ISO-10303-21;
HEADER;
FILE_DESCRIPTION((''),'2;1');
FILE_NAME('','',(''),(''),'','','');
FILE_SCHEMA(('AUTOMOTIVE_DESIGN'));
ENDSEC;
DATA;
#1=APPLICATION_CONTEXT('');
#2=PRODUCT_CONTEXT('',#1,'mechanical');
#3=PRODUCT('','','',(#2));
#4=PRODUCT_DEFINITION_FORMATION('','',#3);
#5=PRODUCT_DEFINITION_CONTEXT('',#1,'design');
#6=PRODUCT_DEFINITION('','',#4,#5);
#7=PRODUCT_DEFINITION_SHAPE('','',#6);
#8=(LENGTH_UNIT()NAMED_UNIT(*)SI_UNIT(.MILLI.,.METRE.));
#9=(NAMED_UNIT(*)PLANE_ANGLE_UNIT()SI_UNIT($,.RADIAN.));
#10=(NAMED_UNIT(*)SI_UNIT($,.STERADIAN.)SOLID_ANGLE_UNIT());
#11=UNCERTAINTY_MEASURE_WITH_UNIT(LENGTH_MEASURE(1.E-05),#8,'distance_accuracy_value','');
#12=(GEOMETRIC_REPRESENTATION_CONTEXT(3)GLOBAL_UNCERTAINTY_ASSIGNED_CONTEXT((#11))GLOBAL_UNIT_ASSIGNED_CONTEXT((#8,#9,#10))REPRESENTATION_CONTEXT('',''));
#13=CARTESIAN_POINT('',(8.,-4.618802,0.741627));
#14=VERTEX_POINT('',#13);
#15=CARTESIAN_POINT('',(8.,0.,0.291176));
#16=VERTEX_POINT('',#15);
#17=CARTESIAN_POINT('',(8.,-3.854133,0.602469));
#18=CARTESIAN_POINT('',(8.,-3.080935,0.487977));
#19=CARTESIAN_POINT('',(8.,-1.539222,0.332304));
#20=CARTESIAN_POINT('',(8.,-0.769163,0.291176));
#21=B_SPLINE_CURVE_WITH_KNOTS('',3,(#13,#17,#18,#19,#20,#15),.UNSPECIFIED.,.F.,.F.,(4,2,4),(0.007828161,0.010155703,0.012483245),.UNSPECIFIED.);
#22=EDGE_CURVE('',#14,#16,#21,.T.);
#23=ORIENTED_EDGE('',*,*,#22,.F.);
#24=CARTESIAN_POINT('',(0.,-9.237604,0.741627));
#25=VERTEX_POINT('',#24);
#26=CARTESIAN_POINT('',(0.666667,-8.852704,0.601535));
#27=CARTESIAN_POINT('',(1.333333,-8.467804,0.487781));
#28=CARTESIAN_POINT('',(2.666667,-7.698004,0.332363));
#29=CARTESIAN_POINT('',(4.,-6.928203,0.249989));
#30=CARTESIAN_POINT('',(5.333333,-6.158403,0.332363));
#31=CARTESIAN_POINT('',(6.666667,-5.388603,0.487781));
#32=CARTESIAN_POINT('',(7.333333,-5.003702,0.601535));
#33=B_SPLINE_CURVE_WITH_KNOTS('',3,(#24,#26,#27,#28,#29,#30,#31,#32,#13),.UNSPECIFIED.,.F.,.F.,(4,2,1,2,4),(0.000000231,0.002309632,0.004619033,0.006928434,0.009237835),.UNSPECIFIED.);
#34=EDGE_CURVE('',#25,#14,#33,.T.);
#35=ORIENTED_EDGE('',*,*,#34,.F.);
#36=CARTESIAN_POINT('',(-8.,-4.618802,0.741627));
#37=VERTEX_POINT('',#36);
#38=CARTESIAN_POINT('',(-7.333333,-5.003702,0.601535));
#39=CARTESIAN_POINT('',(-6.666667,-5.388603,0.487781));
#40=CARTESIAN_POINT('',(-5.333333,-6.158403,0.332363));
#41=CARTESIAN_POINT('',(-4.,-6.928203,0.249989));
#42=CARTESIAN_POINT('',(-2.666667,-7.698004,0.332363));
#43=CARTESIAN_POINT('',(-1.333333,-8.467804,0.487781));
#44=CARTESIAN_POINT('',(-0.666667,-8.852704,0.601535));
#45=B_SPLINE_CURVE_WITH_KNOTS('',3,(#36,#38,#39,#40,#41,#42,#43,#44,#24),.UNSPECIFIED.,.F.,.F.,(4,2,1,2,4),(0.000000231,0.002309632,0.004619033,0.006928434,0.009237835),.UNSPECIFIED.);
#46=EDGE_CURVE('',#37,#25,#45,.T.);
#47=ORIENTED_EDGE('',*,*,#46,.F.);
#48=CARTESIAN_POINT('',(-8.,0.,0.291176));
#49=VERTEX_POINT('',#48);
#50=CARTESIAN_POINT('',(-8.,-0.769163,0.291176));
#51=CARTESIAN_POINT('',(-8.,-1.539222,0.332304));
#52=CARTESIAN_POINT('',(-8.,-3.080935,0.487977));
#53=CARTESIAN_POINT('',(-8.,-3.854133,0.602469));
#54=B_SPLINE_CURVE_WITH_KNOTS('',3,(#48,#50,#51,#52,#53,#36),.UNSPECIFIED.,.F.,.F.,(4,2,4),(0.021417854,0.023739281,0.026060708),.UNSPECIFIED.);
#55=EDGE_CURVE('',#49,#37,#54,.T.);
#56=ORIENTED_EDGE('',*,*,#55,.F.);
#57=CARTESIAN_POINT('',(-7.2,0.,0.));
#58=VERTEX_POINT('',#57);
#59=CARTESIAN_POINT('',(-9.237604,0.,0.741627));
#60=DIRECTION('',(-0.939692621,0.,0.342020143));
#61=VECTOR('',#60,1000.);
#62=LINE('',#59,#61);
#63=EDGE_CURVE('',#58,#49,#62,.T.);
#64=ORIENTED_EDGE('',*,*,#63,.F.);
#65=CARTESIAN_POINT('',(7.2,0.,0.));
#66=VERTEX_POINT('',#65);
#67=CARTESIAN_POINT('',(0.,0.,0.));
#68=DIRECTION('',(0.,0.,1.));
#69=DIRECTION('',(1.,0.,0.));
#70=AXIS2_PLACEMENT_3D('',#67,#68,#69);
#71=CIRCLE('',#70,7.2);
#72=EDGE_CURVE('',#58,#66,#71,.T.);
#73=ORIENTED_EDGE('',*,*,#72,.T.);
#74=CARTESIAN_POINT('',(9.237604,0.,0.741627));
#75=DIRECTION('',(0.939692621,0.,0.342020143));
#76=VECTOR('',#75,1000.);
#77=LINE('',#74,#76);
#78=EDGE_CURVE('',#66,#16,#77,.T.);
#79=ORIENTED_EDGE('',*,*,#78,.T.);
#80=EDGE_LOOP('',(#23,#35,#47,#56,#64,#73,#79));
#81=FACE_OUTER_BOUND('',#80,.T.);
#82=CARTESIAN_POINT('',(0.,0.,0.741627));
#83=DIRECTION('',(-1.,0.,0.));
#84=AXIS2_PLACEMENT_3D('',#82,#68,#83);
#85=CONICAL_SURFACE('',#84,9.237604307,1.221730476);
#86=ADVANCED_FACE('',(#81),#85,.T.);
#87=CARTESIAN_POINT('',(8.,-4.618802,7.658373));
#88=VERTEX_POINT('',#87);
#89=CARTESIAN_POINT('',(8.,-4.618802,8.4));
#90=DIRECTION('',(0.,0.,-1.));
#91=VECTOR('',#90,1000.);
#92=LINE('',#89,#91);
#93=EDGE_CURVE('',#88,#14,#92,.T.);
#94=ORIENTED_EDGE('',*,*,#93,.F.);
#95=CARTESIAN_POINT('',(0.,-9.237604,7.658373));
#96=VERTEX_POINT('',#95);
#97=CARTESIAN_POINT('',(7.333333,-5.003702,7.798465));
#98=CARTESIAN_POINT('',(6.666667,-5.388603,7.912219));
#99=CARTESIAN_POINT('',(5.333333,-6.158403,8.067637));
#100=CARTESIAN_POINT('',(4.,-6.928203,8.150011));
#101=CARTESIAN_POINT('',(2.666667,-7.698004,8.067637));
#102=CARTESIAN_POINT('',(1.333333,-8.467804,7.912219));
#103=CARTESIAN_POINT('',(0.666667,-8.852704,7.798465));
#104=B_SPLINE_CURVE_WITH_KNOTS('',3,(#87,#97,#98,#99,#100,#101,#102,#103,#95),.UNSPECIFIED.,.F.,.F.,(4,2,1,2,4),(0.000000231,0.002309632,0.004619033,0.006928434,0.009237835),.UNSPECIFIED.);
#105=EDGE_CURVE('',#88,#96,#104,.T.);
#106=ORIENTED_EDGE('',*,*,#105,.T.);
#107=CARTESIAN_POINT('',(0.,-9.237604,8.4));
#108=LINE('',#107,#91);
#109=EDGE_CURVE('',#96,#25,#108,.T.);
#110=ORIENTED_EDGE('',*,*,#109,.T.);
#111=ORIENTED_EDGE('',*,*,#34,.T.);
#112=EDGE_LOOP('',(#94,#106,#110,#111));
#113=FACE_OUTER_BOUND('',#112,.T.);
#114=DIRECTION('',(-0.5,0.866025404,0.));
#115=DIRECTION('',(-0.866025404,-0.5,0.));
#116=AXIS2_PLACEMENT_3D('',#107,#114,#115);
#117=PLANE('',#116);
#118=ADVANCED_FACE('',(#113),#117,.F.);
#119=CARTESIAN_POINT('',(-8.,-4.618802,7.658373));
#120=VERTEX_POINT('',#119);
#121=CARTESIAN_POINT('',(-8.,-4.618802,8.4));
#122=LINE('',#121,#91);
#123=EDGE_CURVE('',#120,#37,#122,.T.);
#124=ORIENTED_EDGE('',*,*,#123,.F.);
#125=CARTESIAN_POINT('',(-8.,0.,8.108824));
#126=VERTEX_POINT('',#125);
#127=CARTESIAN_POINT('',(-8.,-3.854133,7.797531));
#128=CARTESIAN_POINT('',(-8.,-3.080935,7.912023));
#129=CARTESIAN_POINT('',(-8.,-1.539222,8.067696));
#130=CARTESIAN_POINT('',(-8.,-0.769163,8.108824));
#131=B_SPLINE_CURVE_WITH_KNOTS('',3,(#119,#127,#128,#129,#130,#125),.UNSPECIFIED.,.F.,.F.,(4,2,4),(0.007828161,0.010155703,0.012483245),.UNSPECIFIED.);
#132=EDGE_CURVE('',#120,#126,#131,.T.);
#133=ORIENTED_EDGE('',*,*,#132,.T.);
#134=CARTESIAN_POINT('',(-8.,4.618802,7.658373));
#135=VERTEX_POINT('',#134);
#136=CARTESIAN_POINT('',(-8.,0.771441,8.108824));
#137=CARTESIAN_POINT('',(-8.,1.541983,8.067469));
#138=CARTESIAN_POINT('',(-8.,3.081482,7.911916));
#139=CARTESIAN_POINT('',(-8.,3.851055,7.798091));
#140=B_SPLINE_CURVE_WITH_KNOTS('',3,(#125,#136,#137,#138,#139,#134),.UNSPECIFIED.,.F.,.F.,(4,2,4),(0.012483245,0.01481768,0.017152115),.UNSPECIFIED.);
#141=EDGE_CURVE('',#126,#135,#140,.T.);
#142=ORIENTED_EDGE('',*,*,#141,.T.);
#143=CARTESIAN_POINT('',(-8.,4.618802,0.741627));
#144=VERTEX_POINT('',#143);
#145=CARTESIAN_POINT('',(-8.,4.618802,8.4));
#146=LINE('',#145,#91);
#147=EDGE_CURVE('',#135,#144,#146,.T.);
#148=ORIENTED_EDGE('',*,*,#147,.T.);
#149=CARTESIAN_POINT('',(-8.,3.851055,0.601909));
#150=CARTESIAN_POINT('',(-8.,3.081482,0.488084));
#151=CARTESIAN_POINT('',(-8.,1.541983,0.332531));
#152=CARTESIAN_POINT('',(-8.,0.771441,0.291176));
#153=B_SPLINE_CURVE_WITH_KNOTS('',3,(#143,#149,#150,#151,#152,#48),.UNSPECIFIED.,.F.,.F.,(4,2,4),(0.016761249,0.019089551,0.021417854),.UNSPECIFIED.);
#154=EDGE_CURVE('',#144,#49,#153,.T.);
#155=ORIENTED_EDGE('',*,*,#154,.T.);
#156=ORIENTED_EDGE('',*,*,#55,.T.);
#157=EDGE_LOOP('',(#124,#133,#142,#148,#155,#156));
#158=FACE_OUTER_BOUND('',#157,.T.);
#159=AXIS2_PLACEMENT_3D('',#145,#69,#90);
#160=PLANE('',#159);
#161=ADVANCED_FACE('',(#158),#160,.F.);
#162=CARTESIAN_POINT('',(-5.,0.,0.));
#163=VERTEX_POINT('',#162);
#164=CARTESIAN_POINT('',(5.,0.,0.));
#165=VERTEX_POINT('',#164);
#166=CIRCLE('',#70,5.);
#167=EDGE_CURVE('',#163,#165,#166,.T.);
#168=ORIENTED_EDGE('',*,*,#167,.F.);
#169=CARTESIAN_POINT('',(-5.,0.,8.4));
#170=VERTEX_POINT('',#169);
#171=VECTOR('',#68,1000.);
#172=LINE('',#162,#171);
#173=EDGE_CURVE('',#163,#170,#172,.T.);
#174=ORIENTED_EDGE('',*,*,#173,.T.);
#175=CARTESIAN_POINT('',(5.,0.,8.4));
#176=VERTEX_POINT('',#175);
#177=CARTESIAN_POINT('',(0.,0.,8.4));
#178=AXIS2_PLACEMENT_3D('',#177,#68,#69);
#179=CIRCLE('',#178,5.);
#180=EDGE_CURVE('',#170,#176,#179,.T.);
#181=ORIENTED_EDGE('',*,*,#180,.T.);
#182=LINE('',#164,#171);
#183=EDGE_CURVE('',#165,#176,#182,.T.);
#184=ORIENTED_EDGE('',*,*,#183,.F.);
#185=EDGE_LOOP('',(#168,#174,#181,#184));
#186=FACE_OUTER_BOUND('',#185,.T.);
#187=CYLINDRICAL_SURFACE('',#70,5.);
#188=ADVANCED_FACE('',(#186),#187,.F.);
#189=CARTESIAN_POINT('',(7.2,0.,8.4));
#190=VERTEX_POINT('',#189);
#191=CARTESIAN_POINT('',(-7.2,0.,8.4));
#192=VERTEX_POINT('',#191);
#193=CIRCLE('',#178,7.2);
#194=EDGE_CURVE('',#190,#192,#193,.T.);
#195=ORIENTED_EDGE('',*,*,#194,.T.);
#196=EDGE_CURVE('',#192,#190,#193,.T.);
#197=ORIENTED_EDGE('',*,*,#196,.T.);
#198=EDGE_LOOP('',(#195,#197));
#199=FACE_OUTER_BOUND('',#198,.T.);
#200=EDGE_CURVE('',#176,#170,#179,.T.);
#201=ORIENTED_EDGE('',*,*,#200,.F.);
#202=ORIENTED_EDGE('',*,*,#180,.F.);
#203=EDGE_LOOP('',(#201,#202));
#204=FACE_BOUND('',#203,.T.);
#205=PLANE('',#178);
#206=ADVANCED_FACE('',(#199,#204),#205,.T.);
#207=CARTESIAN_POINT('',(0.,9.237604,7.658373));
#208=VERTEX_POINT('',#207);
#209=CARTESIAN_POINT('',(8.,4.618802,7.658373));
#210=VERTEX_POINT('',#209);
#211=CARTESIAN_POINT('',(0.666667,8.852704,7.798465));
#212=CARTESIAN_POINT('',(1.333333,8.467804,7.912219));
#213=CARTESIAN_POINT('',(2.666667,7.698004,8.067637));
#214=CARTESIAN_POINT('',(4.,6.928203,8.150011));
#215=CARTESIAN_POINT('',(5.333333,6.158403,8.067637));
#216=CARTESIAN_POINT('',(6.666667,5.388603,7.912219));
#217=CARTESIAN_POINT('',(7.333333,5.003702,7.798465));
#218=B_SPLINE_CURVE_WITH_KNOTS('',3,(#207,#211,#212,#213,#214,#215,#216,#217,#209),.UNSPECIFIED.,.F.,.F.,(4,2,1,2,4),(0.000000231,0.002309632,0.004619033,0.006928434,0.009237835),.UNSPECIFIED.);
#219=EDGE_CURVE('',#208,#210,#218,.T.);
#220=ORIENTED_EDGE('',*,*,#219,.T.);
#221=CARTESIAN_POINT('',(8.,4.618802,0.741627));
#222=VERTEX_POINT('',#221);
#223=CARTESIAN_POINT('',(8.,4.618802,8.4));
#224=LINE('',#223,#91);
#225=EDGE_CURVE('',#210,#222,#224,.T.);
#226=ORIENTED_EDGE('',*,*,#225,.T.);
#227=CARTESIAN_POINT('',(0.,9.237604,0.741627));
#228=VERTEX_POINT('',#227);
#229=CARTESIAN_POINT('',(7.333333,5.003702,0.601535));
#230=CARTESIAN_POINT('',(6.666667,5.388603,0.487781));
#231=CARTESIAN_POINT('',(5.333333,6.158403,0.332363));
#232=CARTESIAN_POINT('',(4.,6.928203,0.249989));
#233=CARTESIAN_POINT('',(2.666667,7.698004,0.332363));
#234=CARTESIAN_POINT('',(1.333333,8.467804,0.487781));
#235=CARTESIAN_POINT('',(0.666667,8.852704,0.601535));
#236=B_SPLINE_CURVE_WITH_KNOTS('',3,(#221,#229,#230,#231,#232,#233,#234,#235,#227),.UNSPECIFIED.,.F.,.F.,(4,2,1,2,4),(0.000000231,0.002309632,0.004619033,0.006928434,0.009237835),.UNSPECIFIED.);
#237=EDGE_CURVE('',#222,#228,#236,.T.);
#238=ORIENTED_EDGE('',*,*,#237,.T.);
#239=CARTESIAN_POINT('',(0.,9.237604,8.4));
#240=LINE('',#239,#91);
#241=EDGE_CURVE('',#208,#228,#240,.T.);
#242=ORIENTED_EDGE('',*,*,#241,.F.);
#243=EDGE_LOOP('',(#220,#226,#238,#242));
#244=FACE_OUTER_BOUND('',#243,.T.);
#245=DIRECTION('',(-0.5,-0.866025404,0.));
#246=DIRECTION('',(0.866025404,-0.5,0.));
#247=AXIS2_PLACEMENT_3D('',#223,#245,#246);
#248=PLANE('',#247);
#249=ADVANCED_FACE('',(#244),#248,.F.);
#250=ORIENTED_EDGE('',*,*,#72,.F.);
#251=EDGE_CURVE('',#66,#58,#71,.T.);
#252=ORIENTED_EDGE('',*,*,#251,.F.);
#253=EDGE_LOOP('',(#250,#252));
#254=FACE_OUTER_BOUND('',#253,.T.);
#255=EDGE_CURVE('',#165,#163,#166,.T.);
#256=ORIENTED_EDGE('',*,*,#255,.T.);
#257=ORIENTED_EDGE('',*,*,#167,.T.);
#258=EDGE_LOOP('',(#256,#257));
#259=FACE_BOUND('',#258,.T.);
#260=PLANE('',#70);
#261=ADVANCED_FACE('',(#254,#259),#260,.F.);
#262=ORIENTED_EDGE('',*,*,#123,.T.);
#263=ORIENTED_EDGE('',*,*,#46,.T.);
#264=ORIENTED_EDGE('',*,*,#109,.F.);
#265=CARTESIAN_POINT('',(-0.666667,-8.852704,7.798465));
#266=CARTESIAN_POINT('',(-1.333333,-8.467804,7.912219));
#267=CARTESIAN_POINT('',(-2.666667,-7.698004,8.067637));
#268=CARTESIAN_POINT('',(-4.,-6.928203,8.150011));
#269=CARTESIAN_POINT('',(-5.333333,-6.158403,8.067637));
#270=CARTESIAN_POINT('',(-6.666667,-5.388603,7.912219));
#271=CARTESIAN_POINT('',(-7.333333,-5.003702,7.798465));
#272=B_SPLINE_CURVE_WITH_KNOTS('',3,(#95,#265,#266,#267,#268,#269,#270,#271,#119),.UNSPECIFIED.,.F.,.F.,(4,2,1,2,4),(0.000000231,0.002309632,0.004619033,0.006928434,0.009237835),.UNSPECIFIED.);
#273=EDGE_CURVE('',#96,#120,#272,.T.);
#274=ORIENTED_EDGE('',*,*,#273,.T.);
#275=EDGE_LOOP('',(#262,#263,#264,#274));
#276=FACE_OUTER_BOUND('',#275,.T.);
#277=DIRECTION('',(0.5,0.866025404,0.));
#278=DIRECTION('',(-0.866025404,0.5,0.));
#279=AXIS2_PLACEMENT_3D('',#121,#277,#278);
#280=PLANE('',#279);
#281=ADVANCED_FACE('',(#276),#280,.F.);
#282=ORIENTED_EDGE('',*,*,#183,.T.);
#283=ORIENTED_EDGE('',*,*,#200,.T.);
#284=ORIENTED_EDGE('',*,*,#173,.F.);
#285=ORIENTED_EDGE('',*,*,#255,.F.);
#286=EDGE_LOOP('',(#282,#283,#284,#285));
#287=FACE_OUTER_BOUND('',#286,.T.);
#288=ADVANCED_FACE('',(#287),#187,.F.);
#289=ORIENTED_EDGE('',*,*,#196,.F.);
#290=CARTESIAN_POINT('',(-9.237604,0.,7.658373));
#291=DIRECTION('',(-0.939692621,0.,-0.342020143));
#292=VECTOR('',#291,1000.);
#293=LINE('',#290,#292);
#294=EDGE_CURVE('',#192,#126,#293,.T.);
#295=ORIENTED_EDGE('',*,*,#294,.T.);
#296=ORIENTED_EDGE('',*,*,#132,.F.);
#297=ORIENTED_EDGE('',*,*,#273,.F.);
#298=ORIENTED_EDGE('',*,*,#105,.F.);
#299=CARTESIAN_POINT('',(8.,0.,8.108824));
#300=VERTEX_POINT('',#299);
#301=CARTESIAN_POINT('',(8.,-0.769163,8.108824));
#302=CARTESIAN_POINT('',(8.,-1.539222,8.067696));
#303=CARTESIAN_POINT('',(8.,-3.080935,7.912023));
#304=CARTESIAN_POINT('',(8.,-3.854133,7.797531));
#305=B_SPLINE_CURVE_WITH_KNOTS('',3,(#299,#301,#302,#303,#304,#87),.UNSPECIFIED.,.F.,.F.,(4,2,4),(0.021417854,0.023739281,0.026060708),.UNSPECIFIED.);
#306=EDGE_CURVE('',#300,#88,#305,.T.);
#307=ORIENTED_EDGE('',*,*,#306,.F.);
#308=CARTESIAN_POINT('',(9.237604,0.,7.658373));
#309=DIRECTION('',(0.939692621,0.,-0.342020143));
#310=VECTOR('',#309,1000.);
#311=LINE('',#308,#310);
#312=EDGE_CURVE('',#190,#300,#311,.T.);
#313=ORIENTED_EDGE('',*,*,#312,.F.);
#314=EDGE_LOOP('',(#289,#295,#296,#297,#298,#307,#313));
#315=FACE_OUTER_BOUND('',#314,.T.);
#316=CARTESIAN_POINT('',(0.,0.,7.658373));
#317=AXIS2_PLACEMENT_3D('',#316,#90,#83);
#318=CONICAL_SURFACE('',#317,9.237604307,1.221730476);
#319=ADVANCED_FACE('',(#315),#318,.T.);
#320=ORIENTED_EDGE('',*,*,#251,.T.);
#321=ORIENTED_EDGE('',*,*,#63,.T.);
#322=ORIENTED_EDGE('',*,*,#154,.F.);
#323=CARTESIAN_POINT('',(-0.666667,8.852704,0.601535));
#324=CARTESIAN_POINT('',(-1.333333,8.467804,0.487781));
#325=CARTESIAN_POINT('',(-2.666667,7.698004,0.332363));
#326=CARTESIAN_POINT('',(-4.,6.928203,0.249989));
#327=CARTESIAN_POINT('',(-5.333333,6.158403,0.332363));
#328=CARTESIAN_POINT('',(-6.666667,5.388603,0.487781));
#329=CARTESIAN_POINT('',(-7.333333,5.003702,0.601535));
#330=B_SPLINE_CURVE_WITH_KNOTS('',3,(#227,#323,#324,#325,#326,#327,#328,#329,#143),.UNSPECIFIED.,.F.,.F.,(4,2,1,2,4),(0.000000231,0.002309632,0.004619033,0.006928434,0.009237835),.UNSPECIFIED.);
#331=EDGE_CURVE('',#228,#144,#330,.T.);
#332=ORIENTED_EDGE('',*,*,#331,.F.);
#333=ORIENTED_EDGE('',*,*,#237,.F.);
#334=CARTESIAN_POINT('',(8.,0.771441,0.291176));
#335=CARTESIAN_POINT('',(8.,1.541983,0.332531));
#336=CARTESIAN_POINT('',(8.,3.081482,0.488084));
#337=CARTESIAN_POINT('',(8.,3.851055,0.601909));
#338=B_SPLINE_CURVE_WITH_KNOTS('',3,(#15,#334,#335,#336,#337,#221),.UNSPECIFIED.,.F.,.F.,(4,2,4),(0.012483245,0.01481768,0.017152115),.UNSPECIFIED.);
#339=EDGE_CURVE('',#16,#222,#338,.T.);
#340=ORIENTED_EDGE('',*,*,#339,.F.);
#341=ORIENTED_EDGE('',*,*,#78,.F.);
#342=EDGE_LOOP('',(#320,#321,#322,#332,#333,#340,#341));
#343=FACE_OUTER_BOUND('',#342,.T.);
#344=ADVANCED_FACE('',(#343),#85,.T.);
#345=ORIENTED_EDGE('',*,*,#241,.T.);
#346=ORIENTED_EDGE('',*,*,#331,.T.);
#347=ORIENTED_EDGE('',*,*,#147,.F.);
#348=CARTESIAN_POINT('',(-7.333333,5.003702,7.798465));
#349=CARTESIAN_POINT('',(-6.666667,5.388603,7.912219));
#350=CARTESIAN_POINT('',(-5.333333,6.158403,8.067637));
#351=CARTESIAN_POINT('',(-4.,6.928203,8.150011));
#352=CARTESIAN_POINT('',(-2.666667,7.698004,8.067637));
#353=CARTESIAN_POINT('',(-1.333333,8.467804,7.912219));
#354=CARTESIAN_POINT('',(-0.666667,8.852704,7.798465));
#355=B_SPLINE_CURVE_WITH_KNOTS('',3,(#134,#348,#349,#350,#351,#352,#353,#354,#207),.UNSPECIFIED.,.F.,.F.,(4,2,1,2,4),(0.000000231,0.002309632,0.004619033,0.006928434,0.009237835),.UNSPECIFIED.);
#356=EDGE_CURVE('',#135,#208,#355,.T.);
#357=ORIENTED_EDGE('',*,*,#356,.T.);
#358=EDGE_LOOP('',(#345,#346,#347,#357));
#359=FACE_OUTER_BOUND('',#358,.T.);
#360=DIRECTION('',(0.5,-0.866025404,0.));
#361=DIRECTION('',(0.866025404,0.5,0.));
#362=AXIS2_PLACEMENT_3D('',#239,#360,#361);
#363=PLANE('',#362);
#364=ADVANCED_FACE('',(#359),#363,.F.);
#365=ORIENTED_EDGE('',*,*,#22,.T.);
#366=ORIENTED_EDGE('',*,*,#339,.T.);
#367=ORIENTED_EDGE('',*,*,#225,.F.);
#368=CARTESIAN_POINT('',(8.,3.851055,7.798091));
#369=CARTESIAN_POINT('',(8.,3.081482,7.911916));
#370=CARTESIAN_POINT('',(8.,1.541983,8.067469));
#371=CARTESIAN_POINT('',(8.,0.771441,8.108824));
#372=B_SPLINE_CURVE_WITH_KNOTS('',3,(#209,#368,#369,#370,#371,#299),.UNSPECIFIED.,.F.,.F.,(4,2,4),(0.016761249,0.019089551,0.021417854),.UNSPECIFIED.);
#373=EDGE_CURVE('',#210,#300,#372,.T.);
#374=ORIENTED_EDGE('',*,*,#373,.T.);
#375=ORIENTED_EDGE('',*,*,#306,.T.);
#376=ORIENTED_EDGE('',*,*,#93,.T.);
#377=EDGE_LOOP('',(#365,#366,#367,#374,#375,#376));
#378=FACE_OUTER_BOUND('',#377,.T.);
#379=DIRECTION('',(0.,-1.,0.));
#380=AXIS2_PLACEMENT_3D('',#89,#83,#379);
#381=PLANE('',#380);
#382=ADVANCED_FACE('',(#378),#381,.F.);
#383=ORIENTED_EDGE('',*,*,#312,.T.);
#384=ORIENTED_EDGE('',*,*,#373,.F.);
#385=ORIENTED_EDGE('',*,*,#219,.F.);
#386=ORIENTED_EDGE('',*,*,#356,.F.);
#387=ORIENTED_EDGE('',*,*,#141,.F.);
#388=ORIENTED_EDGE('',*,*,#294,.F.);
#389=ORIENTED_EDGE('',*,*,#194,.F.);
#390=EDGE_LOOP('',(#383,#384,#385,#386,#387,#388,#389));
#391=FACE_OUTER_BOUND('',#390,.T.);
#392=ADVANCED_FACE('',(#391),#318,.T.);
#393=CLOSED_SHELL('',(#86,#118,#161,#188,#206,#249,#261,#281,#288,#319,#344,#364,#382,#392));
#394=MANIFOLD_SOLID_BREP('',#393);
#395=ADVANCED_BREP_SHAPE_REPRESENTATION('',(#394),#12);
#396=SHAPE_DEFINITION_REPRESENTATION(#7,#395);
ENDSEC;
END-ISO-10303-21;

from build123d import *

# Parameters (mm, degrees)
BOSS_EXTRUDE1_DEPTH = 8.4
SKETCH5_R           = 5
CUT_EXTRUDE1_DEPTH  = 15.828800806


with BuildPart() as part:
    # Sketch1 → Boss-Extrude1 (new body)
    with BuildSketch(Plane.XY):
        Polygon((0, 9.237604307), (-8, 4.618802154), (-8, -4.618802154), (0, -9.237604307), (8, -4.618802154), (8, 4.618802154), align=None)
    extrude(amount=BOSS_EXTRUDE1_DEPTH)

    # Sketch4 → Cut-Revolve1 (revolve, cut)
    with BuildSketch(Plane(origin=(0, 0, 0), x_dir=(0, 0, -1), z_dir=(1, 0, 0)), mode=Mode.PRIVATE) as cut_revolve1_sk:
        Polygon((-8.4, -7.2), (-7.658372683, -9.237604307), (-8.4, -9.237604307), align=None)
    cut_revolve1 = revolve(cut_revolve1_sk.sketch.rotate(Axis((0, 0, 8.4), (0, 0, -1)), 119.999999987), axis=Axis((0, 0, 8.4), (0, 0, -1)), mode=Mode.SUBTRACT)

    # Mirror1: Cut-Revolve1 across plane
    add(cut_revolve1.mirror(Plane.XY.offset(4.2)), mode=Mode.SUBTRACT)

    # Sketch5 → Cut-Extrude1 (cut, through all)
    with BuildSketch(Plane.XY.offset(8.4)):
        Circle(SKETCH5_R)
    extrude(amount=-CUT_EXTRUDE1_DEPTH, mode=Mode.SUBTRACT)


solid = part.part
